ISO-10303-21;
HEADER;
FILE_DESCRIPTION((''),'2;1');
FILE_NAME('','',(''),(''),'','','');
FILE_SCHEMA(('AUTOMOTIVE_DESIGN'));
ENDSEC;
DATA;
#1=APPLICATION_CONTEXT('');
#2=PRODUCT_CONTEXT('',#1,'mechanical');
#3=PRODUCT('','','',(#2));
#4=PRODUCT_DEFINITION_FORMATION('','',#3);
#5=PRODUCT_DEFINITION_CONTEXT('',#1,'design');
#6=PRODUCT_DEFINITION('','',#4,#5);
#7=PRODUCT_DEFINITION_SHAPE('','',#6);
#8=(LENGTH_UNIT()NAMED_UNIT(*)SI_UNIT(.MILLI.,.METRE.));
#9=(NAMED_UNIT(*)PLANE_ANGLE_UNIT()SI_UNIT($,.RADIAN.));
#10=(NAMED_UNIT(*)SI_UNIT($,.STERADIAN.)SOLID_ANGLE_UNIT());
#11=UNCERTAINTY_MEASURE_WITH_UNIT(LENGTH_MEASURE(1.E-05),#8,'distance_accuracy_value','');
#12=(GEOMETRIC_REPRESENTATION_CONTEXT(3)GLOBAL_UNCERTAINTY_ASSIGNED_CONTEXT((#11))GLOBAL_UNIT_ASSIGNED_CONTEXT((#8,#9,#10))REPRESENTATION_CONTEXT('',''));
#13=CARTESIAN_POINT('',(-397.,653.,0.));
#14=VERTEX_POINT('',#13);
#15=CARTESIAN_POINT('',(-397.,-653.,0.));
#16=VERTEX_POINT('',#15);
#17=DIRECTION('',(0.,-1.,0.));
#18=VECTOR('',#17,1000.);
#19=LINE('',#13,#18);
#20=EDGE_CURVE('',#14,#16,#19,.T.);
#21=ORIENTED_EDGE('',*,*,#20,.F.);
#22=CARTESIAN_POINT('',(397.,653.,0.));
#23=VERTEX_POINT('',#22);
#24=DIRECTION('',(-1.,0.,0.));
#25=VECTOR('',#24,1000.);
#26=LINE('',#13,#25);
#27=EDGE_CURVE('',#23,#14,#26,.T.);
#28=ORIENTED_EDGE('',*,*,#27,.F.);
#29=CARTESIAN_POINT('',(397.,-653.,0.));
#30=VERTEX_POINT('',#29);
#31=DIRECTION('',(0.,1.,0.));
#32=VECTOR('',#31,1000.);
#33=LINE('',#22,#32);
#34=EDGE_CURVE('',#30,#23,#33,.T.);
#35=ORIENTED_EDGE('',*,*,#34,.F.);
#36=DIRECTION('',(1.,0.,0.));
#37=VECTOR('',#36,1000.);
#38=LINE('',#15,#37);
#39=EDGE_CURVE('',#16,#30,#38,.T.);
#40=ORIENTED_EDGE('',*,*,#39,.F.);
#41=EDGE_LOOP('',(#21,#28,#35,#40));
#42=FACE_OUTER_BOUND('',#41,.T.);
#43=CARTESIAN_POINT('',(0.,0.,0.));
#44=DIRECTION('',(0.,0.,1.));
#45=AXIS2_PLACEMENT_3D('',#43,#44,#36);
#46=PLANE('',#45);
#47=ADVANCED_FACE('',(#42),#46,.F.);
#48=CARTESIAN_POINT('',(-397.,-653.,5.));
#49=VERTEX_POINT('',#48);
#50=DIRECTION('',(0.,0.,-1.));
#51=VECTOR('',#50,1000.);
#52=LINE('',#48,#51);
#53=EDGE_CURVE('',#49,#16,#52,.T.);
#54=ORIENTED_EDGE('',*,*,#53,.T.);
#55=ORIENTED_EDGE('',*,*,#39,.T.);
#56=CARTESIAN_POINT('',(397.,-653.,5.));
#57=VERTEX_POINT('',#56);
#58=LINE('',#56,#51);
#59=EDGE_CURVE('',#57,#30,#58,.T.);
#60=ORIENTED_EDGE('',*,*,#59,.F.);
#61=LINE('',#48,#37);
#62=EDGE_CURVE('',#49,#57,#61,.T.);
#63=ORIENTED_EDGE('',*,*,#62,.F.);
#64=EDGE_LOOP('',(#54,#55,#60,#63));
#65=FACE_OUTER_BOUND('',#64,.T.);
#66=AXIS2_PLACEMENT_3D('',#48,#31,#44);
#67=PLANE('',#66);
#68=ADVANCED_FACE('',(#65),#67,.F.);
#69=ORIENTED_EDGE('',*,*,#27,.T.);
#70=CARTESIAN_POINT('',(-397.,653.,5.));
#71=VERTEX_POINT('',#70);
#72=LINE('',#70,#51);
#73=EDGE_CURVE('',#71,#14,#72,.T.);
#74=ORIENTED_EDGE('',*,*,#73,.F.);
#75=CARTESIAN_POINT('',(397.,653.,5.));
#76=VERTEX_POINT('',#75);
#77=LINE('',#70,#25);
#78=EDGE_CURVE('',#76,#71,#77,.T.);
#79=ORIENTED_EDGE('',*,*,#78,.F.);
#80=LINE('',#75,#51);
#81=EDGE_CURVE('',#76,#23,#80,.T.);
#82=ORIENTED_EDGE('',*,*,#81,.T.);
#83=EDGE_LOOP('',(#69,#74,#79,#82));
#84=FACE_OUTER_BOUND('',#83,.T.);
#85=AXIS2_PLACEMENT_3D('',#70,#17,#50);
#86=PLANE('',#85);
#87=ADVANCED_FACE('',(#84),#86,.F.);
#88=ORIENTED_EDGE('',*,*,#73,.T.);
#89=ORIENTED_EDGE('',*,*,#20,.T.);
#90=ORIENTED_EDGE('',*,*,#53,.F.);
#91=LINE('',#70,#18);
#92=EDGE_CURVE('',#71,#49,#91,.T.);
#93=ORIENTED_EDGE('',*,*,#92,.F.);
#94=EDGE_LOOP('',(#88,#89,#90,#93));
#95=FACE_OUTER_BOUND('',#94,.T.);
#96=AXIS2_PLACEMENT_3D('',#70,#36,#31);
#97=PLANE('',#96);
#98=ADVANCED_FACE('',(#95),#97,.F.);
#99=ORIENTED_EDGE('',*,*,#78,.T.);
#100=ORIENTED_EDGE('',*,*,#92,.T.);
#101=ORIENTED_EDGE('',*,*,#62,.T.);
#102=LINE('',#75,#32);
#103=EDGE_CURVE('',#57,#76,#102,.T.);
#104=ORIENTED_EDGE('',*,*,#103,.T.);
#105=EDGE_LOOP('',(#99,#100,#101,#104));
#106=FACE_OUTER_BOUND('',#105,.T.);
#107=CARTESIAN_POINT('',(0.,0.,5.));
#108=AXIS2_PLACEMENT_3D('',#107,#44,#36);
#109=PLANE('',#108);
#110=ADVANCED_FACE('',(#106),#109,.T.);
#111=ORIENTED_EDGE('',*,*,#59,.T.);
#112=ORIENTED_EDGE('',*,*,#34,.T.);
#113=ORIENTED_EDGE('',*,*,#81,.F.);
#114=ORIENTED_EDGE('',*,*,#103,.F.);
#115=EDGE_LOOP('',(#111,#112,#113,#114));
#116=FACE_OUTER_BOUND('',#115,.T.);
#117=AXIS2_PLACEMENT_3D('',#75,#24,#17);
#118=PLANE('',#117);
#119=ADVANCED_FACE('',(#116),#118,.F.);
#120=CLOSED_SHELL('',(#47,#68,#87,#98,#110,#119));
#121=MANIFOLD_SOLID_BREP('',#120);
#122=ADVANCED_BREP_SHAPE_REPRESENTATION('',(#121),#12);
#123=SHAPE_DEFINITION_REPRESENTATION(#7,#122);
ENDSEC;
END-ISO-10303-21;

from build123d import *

# Parameters (mm, degrees)
SKETCH_1_W      = 794
SKETCH_1_H      = 1306
EXTRUDE_1_DEPTH = 5


with BuildPart() as part:
    # 草图1 → 凸台-拉伸1 (new body)
    with BuildSketch(Plane.XY):
        Rectangle(SKETCH_1_W, SKETCH_1_H)
    extrude(amount=EXTRUDE_1_DEPTH)


solid = part.part
